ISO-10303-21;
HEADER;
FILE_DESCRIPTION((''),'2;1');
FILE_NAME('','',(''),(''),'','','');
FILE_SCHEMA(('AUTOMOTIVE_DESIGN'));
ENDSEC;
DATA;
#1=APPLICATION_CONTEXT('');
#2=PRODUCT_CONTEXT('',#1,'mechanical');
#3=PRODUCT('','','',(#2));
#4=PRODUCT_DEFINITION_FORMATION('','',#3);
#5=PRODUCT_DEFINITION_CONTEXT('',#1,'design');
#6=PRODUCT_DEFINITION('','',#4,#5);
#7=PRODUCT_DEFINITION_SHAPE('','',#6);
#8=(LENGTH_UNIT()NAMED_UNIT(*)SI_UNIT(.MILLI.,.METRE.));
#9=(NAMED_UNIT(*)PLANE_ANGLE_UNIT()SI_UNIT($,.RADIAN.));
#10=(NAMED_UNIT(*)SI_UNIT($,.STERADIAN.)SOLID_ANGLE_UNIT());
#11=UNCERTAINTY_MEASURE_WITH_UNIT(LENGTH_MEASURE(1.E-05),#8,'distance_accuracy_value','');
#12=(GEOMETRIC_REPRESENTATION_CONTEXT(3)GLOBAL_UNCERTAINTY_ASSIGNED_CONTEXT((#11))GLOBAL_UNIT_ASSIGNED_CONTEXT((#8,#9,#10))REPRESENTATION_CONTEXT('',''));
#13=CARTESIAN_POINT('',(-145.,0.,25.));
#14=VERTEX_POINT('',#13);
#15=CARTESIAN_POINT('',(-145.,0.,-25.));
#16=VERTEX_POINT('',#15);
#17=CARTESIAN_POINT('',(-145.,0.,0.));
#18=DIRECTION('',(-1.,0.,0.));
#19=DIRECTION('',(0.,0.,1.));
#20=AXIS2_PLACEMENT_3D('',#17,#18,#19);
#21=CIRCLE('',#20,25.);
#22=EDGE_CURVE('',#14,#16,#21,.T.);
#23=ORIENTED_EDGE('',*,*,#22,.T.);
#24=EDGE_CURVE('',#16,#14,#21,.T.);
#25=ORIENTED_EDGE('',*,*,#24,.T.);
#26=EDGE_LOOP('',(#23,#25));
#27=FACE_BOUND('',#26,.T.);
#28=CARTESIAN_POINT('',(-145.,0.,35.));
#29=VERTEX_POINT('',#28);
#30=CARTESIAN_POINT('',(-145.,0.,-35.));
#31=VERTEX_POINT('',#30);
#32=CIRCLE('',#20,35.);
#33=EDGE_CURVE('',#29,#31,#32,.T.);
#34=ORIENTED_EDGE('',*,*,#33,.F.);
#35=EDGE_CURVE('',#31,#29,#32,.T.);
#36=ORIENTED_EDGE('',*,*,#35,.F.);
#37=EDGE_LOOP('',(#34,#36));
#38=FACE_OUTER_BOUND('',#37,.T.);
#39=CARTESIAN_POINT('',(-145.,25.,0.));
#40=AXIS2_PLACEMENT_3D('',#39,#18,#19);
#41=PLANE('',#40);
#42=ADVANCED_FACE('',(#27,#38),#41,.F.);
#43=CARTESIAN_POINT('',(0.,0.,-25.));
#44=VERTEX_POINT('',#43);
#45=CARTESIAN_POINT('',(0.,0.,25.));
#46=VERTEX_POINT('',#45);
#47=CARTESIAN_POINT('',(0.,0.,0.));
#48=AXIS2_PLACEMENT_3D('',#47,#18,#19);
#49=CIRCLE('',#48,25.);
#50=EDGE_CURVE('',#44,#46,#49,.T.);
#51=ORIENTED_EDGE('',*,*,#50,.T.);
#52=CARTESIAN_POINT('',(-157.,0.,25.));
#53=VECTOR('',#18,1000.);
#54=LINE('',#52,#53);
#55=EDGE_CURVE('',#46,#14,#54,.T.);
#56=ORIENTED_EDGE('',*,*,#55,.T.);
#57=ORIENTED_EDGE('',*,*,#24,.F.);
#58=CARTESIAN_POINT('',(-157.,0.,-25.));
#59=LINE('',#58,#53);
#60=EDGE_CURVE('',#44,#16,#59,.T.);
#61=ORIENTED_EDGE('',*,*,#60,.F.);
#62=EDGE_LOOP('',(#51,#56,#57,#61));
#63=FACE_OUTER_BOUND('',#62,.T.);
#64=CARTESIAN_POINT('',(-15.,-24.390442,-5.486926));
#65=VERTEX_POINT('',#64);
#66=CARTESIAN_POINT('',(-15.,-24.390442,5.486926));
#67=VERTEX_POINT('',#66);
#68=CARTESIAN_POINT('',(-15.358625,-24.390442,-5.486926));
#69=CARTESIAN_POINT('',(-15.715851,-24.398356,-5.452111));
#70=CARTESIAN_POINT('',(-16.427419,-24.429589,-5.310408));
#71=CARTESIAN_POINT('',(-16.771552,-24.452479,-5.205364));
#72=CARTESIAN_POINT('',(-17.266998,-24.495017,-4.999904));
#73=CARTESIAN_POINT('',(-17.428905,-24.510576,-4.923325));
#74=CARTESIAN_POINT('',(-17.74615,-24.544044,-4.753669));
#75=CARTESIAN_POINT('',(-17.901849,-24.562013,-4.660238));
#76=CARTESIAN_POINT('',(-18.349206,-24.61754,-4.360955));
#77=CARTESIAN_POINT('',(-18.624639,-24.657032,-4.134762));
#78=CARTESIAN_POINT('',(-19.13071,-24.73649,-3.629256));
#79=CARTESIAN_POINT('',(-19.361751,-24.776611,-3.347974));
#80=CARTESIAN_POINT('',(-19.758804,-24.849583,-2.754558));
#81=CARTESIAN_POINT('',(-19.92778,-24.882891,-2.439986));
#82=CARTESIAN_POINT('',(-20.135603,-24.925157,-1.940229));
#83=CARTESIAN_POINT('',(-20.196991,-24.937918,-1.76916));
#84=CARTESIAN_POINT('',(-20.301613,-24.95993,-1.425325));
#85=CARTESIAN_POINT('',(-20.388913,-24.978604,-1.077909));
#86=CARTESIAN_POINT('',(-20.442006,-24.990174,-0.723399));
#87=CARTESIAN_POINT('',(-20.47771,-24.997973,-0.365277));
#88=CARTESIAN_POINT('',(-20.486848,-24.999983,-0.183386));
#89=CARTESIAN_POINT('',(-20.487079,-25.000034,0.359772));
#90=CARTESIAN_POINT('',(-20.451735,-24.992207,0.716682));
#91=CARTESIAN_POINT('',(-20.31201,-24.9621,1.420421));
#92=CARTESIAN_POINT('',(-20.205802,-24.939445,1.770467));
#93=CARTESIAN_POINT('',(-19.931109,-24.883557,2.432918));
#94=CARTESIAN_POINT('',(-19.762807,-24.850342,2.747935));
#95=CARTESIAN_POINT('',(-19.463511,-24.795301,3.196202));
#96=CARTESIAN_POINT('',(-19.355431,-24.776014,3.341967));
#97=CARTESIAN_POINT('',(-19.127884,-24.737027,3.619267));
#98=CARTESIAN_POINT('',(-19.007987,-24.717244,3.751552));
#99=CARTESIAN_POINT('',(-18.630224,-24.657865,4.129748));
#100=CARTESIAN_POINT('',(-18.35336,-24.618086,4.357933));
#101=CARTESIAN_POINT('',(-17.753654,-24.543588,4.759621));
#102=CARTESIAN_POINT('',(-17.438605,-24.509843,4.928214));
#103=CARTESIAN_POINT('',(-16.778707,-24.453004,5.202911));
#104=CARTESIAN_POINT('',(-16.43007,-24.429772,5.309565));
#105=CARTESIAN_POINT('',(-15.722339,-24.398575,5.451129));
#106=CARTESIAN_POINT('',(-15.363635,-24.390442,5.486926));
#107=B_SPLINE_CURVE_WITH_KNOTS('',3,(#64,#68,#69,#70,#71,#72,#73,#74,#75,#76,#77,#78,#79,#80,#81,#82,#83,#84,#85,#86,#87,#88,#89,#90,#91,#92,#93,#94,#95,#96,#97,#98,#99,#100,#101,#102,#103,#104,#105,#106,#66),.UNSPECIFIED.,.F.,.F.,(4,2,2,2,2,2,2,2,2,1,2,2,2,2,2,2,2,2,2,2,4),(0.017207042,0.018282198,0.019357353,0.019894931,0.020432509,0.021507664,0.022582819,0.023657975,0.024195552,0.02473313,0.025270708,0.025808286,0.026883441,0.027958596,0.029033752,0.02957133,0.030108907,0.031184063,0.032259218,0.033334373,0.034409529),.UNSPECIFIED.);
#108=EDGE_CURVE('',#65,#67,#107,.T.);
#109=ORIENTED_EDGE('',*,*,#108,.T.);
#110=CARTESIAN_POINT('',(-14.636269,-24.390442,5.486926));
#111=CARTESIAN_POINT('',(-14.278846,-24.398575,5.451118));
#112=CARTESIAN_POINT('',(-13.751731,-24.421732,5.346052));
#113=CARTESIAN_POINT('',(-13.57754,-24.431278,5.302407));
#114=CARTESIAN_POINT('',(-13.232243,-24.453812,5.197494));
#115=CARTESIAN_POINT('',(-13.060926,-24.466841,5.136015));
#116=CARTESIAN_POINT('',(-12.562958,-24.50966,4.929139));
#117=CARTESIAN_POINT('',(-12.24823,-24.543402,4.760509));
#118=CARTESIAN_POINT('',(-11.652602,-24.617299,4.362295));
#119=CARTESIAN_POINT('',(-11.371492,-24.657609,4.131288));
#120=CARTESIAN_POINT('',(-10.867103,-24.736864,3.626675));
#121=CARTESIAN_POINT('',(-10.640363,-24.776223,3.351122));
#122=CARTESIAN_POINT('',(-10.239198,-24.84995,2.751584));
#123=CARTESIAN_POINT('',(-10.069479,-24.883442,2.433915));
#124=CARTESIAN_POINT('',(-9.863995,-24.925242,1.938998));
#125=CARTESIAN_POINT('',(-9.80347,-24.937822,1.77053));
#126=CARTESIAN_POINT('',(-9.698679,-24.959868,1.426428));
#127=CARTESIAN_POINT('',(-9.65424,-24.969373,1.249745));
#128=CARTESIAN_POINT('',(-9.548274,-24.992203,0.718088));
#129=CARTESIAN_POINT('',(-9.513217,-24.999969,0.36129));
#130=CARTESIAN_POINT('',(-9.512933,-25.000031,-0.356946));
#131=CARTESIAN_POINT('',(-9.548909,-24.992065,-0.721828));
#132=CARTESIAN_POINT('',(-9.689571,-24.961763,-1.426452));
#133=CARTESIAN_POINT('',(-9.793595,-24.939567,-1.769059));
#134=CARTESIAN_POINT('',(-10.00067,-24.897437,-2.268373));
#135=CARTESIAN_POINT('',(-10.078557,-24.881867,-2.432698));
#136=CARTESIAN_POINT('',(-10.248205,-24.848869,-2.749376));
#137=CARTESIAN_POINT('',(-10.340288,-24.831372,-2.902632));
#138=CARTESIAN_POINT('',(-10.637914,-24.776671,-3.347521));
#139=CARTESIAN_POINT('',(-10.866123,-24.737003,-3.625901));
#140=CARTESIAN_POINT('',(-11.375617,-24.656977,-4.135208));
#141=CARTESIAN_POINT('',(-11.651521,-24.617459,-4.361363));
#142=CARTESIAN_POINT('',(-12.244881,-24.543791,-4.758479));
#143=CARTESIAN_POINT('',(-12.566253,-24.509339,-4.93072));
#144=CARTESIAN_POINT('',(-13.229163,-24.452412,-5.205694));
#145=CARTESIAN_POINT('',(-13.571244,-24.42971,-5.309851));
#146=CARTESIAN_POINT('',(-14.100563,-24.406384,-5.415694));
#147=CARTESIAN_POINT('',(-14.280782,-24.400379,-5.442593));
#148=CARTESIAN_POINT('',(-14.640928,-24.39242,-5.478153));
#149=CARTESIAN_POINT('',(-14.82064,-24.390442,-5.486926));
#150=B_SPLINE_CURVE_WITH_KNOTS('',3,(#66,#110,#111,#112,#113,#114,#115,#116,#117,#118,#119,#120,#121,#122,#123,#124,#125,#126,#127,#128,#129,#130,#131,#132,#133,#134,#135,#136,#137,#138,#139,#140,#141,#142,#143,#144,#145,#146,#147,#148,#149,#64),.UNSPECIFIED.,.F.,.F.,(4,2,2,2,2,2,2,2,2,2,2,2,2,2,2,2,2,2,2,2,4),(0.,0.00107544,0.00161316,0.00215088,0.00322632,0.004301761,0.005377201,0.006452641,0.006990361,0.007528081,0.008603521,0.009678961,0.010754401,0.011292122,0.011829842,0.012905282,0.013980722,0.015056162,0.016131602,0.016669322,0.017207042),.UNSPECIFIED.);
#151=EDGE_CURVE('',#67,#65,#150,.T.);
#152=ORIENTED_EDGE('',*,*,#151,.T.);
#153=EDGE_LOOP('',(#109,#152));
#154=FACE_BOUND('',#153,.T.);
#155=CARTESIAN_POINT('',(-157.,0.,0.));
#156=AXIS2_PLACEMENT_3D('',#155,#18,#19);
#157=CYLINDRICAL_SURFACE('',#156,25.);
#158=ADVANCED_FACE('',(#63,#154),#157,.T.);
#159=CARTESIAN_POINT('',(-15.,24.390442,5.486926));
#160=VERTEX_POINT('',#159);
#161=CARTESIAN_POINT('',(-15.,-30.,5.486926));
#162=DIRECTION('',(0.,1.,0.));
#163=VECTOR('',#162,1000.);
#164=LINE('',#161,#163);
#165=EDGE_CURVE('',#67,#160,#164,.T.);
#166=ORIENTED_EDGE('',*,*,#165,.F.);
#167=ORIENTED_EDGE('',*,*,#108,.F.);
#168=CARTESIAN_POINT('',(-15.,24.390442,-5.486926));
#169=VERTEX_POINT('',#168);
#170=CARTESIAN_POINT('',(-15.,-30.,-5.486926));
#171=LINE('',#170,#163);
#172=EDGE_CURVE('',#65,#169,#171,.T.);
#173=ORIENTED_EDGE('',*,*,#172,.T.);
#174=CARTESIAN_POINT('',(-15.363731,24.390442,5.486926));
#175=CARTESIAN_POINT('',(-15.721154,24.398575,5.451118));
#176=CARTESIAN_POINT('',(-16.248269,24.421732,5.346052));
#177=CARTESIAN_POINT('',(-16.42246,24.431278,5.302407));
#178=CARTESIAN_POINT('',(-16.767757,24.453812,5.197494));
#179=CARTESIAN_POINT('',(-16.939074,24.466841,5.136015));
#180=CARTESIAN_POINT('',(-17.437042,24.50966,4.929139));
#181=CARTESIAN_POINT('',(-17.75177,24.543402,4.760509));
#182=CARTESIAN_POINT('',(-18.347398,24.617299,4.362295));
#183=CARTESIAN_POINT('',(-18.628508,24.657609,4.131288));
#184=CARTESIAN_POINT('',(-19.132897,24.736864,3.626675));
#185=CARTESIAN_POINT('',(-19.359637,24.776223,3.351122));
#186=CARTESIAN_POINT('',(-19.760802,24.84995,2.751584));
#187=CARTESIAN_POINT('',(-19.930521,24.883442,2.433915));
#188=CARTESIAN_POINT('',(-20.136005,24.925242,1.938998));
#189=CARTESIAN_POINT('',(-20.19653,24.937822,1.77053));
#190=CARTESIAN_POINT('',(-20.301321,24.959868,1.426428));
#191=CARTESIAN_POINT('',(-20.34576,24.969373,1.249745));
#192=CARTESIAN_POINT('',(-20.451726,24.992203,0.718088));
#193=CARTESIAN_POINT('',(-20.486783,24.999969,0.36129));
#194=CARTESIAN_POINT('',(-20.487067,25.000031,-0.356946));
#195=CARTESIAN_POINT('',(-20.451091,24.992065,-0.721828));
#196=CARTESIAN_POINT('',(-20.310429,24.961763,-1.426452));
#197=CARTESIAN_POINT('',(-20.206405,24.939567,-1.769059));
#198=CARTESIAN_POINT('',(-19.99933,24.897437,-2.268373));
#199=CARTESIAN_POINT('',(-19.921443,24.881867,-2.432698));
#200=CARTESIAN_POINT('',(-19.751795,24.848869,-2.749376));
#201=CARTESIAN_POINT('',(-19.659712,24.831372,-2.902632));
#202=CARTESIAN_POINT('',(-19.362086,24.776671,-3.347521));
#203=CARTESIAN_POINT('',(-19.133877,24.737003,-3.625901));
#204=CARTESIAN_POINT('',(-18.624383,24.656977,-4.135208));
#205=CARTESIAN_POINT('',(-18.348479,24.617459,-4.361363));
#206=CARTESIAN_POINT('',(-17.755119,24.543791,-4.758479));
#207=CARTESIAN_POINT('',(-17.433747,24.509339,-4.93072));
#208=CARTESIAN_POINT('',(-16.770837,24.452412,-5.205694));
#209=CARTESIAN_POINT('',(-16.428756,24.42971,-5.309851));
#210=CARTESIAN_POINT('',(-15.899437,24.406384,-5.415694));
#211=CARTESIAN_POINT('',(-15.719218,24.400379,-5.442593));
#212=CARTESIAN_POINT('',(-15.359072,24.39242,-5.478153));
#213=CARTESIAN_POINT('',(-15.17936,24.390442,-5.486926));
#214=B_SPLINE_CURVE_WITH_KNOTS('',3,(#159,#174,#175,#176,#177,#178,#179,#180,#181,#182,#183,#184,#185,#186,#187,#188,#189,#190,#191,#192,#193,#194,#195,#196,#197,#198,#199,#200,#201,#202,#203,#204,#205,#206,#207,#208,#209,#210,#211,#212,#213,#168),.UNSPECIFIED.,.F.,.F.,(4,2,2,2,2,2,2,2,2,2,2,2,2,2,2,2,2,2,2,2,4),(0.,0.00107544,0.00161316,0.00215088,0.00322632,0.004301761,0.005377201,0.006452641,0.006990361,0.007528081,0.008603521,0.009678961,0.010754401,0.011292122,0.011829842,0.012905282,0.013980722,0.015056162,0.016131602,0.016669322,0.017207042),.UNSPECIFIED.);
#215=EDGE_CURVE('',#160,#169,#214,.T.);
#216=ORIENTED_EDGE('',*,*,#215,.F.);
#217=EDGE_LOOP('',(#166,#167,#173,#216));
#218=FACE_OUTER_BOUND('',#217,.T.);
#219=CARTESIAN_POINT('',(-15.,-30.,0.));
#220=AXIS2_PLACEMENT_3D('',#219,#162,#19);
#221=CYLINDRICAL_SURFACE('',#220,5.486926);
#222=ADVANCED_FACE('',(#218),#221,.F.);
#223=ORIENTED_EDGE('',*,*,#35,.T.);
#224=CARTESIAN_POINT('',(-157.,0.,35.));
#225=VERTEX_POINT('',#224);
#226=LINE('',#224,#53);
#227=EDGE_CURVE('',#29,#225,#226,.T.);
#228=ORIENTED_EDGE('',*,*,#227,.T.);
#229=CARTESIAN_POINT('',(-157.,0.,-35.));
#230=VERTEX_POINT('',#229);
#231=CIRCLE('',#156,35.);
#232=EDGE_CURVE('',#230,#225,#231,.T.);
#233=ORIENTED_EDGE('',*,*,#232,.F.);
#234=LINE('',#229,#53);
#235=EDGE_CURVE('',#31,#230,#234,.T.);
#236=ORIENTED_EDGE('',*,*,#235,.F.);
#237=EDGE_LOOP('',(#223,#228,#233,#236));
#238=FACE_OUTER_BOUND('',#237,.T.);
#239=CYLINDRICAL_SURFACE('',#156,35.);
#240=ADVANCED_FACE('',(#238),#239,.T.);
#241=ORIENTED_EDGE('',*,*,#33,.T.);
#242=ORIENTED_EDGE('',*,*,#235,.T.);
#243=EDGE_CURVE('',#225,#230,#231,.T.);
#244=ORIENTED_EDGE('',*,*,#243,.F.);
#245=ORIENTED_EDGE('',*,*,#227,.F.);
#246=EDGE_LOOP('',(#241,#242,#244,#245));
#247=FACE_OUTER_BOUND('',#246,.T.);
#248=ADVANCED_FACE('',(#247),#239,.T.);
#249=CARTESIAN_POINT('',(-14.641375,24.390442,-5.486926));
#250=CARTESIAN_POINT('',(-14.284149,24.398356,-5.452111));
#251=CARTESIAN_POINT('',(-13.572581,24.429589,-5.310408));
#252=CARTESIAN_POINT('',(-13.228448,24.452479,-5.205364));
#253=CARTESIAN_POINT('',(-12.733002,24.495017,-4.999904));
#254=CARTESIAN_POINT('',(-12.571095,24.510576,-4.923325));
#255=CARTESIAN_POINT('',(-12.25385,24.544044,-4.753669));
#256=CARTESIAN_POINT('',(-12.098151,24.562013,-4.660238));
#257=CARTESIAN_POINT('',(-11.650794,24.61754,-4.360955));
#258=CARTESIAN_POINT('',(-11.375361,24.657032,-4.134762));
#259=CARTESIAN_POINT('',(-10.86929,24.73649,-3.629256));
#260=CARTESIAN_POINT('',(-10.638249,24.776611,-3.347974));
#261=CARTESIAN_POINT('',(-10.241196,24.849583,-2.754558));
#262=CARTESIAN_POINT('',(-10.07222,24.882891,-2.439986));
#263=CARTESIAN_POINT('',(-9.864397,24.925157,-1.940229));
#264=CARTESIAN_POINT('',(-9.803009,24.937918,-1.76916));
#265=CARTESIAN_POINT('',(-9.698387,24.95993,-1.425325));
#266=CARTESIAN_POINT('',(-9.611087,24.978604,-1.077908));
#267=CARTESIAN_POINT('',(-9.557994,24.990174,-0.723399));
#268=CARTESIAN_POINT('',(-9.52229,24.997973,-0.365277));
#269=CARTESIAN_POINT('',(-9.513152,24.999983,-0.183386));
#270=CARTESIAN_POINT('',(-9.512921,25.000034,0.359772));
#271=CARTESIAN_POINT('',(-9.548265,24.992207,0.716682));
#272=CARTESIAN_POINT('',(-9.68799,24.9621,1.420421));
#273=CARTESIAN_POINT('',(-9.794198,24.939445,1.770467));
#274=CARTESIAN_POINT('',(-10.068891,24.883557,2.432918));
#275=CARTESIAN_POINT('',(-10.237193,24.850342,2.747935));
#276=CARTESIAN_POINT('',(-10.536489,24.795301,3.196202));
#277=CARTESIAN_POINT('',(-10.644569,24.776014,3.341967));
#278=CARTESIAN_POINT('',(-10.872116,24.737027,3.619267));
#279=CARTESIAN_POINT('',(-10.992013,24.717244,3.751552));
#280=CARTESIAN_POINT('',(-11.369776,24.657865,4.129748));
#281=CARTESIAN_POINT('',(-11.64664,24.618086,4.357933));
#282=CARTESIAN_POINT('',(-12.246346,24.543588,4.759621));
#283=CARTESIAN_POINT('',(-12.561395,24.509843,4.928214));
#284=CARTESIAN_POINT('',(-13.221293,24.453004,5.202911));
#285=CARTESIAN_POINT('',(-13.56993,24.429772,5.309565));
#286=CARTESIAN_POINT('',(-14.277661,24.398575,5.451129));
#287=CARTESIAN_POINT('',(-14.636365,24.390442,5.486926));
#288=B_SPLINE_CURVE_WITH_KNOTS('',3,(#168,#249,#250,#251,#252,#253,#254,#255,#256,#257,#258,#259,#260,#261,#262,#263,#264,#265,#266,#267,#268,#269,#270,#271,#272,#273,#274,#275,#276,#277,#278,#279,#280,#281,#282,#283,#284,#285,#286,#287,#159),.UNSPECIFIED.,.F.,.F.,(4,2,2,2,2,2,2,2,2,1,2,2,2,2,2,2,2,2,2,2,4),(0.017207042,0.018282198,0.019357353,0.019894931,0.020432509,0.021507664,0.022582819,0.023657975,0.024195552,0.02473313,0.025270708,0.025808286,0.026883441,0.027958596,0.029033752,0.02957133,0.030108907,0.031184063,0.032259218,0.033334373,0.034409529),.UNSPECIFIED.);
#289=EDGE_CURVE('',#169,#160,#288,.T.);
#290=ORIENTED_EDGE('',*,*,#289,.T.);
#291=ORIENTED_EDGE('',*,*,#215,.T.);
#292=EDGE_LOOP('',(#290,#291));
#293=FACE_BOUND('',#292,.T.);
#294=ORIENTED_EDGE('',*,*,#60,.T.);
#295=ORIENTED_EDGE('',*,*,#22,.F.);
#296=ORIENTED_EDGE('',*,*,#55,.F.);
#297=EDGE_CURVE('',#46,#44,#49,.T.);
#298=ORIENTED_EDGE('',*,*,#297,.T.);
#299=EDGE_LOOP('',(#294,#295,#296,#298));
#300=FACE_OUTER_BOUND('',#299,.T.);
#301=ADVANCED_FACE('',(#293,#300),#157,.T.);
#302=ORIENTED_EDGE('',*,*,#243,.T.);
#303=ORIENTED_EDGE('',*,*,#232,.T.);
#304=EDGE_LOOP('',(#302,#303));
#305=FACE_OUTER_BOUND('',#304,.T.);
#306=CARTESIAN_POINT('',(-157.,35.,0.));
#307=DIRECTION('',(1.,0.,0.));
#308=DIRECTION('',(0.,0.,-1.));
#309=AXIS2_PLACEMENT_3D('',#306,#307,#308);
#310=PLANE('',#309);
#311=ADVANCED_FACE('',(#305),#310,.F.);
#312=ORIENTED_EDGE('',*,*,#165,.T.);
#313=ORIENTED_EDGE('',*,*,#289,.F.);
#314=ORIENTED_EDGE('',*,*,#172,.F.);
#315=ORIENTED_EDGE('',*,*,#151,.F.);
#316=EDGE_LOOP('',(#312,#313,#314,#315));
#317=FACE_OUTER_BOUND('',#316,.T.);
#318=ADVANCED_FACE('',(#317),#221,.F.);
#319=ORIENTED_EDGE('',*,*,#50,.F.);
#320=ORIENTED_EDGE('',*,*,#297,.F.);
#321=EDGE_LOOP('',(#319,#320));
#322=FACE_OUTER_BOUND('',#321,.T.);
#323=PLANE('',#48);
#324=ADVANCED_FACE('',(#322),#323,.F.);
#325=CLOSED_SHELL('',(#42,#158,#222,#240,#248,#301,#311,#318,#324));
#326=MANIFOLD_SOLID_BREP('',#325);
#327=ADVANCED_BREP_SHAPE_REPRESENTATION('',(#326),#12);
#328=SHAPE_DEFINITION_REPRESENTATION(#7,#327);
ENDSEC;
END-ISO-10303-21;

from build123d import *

# Parameters (mm, degrees)
SPLIT_PIN_HOLE_SKETCH_R = 5.486925686
SPLIT_PIN_HOLE_11_DEPTH = 30


with BuildPart() as part:
    # Pin Profile Sketch → Pin Body Revolve (revolve)
    with BuildSketch(Plane.XY, mode=Mode.PRIVATE) as pin_body_revolve_sk:
        Polygon((0, 0), (0, 25), (-145, 25), (-145, 35), (-157, 35), (-157, 0), align=None)
    revolve(pin_body_revolve_sk.sketch.rotate(Axis((-157, 0, 0), (1, 0, 0)), 90), axis=Axis((-157, 0, 0), (1, 0, 0)))

    # Split Pin Hole Sketch → Split Pin Hole Ø11 (cut, symmetric)
    with BuildSketch(Plane(origin=(0, 0, 0), x_dir=(1, 0, 0), z_dir=(0, 1, 0))):
        with Locations(Location((-15, 0, 0), (0, 0, 270))):
            Circle(SPLIT_PIN_HOLE_SKETCH_R)
    extrude(amount=SPLIT_PIN_HOLE_11_DEPTH, both=True, mode=Mode.SUBTRACT)


solid = part.part
